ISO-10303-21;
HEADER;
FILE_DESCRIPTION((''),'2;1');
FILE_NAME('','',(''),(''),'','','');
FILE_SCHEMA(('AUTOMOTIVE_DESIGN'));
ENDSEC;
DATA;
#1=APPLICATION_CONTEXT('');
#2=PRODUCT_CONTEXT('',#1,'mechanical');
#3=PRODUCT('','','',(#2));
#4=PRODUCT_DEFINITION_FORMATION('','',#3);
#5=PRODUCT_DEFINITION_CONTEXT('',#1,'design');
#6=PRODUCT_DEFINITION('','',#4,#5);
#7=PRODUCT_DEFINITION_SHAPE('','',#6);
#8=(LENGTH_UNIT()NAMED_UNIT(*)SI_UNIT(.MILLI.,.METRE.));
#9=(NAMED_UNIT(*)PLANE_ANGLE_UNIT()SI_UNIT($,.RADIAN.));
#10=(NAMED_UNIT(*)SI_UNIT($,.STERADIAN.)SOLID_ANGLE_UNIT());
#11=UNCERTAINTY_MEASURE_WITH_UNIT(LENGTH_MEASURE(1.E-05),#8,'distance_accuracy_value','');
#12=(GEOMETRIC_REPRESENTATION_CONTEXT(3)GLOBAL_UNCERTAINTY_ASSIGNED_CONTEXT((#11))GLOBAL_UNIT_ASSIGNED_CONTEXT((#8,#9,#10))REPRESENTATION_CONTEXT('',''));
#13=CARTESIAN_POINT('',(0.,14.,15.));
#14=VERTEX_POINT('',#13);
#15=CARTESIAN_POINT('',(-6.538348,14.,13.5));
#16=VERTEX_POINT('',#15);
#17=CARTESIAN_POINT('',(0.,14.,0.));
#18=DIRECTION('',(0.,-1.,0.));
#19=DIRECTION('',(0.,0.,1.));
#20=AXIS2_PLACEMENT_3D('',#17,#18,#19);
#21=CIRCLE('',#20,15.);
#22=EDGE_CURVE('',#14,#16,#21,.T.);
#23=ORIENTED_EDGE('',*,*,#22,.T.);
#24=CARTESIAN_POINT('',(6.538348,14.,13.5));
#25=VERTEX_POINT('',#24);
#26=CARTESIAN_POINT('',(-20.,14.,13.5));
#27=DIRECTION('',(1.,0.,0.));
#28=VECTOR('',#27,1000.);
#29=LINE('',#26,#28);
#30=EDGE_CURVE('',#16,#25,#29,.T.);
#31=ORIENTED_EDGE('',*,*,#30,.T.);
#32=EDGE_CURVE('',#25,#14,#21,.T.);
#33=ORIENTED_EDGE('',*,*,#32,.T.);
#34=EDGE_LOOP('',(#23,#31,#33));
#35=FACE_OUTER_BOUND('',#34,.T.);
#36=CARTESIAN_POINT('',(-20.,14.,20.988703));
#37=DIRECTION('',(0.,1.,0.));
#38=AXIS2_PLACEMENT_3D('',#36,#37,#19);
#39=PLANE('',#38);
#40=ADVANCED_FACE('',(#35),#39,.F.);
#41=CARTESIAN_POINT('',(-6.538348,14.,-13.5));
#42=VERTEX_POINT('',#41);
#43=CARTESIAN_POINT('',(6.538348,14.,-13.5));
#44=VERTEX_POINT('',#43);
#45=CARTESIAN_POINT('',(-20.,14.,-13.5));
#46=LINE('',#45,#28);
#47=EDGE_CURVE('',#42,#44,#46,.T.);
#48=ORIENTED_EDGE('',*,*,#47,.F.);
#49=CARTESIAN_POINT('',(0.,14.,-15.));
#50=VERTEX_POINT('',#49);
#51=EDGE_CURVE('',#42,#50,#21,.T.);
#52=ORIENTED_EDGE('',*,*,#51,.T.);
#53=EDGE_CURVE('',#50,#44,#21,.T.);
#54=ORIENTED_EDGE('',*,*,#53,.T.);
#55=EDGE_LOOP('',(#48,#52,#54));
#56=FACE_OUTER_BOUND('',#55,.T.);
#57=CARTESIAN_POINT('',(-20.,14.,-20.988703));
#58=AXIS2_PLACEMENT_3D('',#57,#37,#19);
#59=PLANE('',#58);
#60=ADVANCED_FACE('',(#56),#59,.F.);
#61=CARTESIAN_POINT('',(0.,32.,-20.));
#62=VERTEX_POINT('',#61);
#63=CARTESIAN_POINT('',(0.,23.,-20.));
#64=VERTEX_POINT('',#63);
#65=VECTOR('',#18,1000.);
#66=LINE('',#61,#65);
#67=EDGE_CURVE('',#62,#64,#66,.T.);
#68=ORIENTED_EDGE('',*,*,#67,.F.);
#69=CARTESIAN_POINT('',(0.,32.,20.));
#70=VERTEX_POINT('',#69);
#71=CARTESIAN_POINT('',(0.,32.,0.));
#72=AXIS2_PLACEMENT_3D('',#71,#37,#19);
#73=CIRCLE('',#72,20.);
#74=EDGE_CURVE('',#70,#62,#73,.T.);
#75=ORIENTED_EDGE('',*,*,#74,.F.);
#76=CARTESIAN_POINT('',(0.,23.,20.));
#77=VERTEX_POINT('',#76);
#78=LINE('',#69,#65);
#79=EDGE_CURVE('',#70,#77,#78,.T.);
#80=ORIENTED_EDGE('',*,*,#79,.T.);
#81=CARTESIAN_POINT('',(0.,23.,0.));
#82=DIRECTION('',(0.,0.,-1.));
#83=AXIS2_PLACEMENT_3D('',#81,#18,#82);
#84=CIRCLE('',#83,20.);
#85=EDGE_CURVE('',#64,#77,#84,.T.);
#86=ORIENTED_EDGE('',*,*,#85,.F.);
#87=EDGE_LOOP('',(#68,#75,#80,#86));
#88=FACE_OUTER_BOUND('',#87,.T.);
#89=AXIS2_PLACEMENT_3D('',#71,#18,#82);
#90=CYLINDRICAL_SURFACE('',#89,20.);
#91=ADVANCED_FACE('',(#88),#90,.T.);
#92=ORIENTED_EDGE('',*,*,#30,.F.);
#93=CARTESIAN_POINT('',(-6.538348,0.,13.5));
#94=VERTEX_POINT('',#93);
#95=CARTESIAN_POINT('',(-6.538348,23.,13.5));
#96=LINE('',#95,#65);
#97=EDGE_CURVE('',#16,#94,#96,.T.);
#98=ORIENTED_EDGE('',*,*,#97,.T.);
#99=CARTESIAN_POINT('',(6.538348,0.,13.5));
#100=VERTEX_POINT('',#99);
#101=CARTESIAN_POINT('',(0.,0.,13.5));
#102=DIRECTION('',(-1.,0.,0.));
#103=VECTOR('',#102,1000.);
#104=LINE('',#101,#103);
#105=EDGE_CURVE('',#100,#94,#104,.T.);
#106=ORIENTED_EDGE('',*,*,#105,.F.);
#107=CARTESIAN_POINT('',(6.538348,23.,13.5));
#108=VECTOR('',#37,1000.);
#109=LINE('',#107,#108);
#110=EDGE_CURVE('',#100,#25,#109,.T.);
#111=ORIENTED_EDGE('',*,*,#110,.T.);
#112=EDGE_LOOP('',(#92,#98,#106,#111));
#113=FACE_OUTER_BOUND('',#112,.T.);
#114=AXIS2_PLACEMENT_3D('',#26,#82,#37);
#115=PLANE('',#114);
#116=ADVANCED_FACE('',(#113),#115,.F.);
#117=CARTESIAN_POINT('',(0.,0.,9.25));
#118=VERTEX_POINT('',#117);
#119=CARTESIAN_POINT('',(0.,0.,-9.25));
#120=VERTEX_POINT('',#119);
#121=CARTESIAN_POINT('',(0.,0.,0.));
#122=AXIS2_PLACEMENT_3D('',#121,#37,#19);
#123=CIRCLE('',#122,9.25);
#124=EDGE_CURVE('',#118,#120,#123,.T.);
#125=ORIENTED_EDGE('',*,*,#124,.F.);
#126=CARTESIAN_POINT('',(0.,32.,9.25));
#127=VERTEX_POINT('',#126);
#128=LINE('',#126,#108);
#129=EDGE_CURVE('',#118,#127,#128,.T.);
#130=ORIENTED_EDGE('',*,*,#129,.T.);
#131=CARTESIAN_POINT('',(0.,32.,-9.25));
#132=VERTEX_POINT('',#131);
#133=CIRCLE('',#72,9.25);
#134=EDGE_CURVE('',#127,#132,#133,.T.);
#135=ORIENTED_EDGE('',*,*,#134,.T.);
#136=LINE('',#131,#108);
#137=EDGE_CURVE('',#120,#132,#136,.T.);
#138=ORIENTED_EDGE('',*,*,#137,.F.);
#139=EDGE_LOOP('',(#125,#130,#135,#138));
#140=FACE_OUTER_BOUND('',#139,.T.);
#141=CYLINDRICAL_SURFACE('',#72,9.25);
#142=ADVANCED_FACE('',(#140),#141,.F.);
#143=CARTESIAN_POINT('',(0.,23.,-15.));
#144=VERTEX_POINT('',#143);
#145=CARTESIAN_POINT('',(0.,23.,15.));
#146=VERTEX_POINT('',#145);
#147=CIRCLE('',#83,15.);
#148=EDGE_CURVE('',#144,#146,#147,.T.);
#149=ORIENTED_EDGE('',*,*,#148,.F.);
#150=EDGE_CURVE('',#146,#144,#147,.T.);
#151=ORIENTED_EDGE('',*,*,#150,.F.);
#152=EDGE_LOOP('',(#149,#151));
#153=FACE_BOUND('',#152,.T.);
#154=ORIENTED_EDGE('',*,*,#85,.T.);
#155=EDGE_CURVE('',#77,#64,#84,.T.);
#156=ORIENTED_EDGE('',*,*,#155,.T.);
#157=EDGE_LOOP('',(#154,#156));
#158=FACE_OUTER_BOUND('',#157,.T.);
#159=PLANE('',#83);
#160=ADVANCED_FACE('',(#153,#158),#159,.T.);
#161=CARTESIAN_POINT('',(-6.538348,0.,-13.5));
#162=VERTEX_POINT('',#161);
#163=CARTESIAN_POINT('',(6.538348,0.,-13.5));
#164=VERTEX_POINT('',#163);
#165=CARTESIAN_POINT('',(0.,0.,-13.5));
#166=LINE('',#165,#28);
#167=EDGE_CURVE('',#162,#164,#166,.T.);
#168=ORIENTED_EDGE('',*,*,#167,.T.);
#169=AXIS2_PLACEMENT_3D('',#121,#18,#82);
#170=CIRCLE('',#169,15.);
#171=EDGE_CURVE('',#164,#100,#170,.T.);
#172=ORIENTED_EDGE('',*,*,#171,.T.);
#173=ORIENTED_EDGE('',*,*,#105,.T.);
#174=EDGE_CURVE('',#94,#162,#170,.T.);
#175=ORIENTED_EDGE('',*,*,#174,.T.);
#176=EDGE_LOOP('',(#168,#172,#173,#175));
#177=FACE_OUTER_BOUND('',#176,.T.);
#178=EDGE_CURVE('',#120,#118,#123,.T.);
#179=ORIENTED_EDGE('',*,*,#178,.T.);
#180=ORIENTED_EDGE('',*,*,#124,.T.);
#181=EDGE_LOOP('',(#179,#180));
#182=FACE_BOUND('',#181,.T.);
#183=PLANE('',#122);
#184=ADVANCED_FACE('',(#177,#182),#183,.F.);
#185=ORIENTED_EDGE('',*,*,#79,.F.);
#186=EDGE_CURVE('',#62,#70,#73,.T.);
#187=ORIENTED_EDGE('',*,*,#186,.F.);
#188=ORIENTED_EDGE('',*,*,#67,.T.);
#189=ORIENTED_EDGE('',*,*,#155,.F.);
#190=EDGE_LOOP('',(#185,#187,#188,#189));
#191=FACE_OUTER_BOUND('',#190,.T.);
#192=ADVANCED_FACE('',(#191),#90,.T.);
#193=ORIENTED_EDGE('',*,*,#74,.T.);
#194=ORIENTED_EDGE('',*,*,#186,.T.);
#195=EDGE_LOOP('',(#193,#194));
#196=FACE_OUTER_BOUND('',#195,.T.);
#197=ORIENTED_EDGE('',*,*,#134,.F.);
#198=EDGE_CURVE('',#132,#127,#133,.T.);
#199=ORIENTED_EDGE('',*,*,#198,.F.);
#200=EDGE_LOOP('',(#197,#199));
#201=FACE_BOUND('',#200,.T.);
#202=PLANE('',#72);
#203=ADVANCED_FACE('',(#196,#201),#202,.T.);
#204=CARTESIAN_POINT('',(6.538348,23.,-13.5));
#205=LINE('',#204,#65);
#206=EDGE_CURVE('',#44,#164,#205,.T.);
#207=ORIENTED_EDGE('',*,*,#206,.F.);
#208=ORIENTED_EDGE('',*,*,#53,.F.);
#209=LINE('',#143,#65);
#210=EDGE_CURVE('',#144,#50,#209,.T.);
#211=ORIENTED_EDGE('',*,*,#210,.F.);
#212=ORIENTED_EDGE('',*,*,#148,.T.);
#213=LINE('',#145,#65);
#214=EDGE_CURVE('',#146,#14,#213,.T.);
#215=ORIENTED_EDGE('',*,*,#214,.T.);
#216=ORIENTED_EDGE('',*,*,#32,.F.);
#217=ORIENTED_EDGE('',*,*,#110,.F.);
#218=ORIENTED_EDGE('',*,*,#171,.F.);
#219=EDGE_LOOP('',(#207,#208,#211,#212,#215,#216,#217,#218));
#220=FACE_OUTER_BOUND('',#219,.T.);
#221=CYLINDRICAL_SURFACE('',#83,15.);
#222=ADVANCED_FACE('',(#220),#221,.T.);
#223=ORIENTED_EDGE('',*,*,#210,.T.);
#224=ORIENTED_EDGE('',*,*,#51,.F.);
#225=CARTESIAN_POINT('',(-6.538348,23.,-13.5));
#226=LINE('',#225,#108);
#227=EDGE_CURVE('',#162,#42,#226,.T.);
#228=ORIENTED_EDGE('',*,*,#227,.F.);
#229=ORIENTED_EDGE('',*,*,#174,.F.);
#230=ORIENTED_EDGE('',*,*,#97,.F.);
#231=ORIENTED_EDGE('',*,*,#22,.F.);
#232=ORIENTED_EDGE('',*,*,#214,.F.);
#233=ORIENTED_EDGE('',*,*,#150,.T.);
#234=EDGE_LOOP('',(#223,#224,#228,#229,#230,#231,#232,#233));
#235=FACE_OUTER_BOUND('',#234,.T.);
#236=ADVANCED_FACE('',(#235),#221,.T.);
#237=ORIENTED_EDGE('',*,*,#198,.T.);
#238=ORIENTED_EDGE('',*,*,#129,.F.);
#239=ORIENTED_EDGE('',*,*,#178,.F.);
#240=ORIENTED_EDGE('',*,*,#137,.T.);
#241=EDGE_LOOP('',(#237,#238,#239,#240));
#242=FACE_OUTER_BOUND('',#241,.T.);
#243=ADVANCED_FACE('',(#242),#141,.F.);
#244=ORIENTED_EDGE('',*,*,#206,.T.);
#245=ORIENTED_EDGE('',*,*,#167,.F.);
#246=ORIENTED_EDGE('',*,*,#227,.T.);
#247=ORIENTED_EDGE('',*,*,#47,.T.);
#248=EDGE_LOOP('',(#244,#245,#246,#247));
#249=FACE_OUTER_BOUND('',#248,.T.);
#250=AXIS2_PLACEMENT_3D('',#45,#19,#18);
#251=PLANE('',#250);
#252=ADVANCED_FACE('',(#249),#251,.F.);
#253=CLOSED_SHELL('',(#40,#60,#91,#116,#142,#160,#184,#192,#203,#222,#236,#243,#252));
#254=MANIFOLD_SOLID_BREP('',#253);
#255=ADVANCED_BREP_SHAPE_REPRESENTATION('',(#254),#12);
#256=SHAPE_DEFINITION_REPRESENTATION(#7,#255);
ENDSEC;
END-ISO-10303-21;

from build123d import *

# Parameters (mm, degrees)
SKETCH1_R               = 20
SKETCH1_R_2             = 9
BOSS_EXTRUDE1_DEPTH     = 32
SKETCH2_R               = 25
SKETCH2_R_2             = 15
CUT_EXTRUDE1_DEPTH      = 23
CUT_EXTRUDE2_DEPTH      = 43.708313008
CUT_EXTRUDE2_DEPTH_BACK = 43.708313008
SKETCH3_W               = 7.488703297
SKETCH3_H               = 21.290197802
M20X1_5_TAPPED_HOLE1_D  = 18.5


with BuildPart() as part:
    # Sketch1 → Boss-Extrude1 (new body)
    with BuildSketch(Plane(origin=(0, 0, 0), x_dir=(1, 0, 0), z_dir=(0, 1, 0))):
        with Locations(Location((0, 0, 0), (0, 0, 270))):
            Circle(SKETCH1_R)
        with Locations(Location((0, 0, 0), (0, 0, 270))):
            Circle(SKETCH1_R_2, mode=Mode.SUBTRACT)
    extrude(amount=BOSS_EXTRUDE1_DEPTH)

    # Sketch2 → Cut-Extrude1 (cut)
    with BuildSketch(Plane.XZ):
        Circle(SKETCH2_R)
        with Locations(Location((0, 0, 0), (0, 0, 270))):
            Circle(SKETCH2_R_2, mode=Mode.SUBTRACT)
    extrude(amount=-CUT_EXTRUDE1_DEPTH, mode=Mode.SUBTRACT)

    # Sketch3 → Cut-Extrude2 (cut, two sides: drawn at the far end of the back side and taken through both)
    with BuildSketch(Plane(origin=(0, 0, 0), x_dir=(0, 0, -1), z_dir=(1, 0, 0)).offset(-CUT_EXTRUDE2_DEPTH_BACK)):
        with Locations((-17.244351649, 3.354901099)):
            Rectangle(SKETCH3_W, SKETCH3_H)
        with Locations((17.244351649, 3.354901099)):
            Rectangle(SKETCH3_W, SKETCH3_H)
    extrude(amount=CUT_EXTRUDE2_DEPTH + CUT_EXTRUDE2_DEPTH_BACK, mode=Mode.SUBTRACT)

    # M20x1.5 Tapped Hole1 (through all)
    with Locations(Plane(origin=(0, 32, 0), x_dir=(1, 0, 0), z_dir=(0, 1, 0))):
        with Locations((0, 0)):
            Hole(M20X1_5_TAPPED_HOLE1_D / 2)


solid = part.part
